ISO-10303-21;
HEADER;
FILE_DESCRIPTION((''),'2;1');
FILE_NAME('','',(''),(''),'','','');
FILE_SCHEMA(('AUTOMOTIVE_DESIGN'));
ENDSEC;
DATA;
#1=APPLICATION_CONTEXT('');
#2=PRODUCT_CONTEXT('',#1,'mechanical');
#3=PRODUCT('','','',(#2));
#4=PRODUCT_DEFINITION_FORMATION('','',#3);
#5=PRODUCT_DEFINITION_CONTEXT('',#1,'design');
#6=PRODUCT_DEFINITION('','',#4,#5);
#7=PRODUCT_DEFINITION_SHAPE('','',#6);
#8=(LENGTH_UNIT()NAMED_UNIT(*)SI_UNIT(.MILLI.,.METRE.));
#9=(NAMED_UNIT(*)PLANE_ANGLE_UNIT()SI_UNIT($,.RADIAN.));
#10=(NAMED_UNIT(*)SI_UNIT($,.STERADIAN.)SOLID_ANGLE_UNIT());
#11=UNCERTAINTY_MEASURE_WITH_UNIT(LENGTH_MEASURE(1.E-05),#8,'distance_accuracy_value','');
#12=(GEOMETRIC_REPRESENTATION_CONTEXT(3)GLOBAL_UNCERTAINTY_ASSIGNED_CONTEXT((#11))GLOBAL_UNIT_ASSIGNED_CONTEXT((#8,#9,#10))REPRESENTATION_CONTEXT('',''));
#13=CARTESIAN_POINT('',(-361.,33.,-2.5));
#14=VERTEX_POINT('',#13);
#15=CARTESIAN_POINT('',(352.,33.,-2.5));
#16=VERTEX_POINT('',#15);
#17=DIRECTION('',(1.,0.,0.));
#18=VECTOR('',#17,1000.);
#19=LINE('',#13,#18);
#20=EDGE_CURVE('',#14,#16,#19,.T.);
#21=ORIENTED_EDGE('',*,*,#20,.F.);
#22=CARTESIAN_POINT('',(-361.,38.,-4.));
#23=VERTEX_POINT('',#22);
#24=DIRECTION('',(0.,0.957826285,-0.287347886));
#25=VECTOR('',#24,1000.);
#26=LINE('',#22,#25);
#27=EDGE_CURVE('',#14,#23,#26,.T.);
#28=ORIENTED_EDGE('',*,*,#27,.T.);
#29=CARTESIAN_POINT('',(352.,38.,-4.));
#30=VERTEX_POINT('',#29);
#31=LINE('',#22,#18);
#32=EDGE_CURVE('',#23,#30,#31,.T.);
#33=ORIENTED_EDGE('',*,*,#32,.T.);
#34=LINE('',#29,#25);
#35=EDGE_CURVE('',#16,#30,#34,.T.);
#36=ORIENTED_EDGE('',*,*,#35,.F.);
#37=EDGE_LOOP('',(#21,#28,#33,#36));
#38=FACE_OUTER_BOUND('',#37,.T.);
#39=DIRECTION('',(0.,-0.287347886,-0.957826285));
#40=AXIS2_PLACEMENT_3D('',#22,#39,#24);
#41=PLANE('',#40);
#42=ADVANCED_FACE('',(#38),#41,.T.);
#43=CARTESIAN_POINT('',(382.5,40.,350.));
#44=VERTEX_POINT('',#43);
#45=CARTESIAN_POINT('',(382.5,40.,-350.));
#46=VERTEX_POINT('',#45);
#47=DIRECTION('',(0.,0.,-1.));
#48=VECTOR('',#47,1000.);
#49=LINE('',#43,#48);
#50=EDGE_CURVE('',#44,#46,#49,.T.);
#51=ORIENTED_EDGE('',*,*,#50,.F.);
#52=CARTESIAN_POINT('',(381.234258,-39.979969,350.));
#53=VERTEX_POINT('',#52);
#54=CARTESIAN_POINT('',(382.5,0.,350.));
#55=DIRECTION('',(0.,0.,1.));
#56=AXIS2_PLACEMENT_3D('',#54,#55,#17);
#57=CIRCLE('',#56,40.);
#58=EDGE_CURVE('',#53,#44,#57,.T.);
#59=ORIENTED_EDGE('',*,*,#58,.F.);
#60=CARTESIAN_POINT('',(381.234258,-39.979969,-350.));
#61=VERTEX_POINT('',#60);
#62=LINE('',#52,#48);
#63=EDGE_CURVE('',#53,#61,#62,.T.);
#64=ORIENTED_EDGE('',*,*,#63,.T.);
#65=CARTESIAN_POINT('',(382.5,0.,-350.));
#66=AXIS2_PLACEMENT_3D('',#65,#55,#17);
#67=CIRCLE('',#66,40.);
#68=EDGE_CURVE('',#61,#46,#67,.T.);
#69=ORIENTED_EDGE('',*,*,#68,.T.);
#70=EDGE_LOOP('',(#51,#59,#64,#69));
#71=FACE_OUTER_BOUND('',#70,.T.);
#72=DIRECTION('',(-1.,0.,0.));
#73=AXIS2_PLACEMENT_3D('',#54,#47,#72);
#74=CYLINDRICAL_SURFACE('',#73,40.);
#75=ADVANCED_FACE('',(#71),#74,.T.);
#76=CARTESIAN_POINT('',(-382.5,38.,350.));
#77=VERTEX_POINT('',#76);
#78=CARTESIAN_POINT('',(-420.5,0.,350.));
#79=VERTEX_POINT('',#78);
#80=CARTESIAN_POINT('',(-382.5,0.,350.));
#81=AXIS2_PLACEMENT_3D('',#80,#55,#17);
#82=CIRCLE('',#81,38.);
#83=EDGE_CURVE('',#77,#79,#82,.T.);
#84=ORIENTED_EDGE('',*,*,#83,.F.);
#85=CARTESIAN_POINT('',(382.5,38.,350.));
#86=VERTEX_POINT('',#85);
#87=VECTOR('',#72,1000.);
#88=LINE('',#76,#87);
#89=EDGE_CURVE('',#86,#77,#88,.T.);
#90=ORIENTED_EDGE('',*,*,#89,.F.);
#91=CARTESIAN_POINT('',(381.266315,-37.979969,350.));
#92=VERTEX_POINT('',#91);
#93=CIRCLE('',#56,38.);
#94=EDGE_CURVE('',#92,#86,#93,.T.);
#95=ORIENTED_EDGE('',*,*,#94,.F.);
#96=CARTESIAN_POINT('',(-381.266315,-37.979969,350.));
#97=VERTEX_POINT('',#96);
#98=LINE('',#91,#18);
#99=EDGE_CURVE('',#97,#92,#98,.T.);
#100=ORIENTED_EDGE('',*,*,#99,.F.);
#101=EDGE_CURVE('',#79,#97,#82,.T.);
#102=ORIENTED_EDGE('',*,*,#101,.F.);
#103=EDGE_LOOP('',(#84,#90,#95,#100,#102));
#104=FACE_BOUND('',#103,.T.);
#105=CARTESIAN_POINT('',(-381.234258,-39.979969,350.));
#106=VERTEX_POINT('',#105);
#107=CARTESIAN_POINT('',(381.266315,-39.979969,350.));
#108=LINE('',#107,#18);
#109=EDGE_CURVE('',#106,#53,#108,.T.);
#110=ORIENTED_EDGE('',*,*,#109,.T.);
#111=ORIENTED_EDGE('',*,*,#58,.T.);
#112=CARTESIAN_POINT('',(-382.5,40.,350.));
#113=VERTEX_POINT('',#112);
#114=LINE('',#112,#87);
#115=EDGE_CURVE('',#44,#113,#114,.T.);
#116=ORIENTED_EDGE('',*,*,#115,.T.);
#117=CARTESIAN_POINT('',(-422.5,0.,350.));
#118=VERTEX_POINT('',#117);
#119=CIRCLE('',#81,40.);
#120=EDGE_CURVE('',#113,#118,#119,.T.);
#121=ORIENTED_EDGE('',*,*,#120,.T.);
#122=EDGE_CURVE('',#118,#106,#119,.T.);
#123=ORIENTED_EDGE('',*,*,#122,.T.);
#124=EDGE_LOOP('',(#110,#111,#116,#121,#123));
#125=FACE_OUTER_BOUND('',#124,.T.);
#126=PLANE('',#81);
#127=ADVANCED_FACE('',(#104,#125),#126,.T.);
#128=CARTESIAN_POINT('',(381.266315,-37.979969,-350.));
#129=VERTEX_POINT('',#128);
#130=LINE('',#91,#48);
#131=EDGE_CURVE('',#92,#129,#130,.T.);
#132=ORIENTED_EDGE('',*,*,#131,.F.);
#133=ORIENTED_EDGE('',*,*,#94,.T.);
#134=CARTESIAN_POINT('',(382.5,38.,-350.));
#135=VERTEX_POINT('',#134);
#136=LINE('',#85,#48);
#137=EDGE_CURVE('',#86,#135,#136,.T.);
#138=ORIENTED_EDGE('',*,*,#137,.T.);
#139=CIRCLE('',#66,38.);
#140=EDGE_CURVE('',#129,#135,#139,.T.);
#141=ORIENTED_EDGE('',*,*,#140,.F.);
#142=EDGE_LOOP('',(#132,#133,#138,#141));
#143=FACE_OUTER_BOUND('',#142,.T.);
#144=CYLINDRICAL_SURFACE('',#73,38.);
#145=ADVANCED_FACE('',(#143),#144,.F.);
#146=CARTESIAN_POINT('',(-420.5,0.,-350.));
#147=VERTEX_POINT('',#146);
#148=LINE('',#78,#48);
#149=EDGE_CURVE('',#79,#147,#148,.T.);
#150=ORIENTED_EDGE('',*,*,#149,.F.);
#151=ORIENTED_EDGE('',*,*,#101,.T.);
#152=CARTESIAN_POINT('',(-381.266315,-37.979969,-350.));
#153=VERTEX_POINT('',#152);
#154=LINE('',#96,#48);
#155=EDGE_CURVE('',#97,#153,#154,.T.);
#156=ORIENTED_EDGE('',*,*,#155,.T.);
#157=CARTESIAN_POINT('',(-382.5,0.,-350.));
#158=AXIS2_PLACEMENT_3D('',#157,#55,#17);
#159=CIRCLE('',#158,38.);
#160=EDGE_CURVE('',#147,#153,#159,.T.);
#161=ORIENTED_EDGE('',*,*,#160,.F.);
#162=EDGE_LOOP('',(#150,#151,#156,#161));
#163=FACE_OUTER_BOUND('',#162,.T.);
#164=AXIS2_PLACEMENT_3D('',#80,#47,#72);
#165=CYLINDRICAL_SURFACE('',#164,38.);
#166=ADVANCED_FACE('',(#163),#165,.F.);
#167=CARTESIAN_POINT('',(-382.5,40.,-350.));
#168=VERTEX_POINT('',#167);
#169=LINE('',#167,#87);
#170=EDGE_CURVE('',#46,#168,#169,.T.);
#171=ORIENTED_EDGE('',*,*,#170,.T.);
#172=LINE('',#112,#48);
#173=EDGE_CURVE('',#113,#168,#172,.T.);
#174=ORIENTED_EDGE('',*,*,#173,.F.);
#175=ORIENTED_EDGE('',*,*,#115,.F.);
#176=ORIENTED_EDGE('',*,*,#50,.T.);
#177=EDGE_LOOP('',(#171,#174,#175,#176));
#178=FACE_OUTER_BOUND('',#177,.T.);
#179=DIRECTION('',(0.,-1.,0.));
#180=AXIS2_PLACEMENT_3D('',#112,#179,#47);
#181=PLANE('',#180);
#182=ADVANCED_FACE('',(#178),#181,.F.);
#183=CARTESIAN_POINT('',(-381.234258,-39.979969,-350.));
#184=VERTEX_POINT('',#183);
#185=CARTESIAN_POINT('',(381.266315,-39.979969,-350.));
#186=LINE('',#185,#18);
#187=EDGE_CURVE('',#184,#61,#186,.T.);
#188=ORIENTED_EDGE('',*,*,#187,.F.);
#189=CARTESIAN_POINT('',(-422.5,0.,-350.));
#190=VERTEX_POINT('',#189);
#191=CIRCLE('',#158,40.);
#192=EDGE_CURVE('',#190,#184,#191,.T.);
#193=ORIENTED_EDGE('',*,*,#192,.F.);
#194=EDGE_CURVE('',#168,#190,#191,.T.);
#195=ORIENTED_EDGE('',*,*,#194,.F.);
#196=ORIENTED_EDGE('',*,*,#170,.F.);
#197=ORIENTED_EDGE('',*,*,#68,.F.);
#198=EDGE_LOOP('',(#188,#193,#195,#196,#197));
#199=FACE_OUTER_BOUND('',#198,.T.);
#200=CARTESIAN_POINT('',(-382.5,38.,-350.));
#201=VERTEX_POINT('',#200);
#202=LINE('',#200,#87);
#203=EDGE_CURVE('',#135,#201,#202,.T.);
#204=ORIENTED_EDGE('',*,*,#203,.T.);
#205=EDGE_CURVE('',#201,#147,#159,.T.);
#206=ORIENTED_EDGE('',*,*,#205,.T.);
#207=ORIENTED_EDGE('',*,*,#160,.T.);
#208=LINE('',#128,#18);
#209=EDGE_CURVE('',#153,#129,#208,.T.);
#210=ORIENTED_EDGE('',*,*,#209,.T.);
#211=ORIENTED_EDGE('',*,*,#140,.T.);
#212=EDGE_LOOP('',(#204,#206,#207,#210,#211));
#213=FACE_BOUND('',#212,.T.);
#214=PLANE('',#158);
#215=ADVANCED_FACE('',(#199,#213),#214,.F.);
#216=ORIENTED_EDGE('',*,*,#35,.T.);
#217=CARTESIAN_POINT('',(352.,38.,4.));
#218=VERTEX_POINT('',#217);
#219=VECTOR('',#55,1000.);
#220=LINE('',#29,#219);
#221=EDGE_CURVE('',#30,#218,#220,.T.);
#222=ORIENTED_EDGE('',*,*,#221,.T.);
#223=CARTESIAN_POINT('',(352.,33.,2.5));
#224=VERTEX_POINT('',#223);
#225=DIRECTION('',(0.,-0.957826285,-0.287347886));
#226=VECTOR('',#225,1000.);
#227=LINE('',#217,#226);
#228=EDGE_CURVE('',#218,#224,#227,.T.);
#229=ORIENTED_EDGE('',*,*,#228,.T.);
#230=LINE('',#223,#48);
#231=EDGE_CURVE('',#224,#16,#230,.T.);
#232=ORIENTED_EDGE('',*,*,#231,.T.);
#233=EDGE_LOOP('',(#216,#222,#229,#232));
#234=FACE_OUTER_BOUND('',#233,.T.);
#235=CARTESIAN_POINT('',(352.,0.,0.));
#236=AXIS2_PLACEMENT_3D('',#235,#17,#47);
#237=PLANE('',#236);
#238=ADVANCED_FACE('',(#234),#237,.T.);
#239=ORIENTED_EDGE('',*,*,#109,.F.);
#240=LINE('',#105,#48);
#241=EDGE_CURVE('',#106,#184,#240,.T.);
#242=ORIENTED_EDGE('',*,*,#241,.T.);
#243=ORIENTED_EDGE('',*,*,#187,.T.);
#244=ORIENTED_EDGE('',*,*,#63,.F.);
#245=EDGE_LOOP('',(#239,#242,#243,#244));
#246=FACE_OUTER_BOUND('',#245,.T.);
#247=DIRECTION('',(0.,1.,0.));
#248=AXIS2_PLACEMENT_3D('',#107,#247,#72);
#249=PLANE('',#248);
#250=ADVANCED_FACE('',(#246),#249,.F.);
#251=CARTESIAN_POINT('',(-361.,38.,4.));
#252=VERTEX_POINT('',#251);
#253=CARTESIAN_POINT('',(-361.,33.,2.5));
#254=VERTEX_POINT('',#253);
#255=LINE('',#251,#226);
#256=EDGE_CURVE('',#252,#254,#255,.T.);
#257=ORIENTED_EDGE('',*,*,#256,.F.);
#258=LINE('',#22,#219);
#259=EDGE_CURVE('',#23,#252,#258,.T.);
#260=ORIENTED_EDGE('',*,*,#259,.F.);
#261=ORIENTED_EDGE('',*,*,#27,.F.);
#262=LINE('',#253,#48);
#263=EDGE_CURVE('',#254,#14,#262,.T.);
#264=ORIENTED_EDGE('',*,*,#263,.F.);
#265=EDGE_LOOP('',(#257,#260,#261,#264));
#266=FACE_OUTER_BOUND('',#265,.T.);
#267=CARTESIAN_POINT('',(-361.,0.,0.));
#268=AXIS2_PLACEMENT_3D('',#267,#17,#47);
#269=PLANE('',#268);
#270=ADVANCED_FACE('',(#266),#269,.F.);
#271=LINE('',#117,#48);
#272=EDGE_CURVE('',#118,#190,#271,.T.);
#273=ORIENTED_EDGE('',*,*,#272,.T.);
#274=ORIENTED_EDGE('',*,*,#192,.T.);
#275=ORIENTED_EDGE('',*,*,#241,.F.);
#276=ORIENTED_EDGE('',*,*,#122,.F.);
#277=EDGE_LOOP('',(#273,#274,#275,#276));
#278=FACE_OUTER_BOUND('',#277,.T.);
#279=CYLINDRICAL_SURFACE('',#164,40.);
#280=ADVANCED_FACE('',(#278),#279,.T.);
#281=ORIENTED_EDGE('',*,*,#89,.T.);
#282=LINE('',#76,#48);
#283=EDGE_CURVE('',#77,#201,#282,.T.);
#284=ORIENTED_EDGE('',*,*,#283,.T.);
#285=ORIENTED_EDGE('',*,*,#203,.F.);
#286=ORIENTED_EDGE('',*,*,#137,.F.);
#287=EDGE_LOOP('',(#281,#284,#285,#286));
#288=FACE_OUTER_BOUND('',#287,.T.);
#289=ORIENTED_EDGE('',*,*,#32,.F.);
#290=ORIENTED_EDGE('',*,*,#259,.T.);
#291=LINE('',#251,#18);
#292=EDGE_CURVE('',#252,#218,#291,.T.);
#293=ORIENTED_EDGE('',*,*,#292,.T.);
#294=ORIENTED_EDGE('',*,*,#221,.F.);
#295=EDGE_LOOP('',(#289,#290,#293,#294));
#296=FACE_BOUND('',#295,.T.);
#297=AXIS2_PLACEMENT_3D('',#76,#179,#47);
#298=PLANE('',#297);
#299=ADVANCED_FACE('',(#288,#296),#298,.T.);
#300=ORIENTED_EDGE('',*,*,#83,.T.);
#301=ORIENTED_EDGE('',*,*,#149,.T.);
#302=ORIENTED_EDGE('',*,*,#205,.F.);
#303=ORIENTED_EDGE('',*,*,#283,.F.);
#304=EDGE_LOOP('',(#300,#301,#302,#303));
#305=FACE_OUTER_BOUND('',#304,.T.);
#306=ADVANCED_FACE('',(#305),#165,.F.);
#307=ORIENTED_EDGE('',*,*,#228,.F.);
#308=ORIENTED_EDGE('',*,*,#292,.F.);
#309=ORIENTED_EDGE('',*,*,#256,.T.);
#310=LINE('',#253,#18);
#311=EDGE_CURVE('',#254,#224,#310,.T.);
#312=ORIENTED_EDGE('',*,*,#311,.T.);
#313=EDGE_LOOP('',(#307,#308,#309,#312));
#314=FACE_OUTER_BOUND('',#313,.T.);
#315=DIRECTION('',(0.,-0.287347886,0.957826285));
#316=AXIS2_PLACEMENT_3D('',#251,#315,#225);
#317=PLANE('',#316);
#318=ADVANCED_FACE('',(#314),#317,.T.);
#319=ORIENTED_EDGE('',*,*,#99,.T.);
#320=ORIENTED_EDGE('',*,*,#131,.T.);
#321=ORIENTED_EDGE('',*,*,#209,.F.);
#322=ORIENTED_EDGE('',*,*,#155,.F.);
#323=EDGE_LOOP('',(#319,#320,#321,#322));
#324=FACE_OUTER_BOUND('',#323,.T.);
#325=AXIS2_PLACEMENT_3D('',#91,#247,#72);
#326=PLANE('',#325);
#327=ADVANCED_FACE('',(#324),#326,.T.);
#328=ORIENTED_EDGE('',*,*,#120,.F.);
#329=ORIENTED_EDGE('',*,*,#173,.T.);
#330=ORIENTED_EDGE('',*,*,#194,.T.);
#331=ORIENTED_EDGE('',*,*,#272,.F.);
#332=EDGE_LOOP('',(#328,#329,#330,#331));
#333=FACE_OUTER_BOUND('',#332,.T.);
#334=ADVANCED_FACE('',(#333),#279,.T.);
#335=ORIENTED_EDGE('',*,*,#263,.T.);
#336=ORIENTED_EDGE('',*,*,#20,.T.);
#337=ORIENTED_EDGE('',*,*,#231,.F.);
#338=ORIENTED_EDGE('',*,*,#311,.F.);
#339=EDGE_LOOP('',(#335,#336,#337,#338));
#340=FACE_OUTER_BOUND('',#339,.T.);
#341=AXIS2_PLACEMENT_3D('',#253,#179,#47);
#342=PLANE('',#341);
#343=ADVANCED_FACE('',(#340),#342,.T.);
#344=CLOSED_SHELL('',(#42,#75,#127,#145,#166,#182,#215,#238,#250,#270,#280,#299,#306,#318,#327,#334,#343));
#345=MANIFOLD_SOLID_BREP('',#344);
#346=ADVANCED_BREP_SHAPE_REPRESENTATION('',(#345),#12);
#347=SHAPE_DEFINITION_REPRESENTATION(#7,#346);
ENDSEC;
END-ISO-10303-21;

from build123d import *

# Parameters (mm, degrees)
EXTRUDE_1_DEPTH      = 350
EXTRUDE_2_DEPTH      = 352
EXTRUDE_2_DEPTH_BACK = 361


with BuildPart() as part:
    # 草图1 → 拉伸-薄壁1 (new, symmetric)
    with BuildSketch(Plane.XY):
        with BuildLine():
            Line((381.234257801, -39.979968693), (-381.234257801, -39.979968693))
            ThreePointArc((-381.234257801, -39.979968693), (-422.49499186, -0.632950347), (-382.5, 40))
            Line((-382.5, 40), (382.5, 40))
            ThreePointArc((382.5, 40), (422.49499186, -0.632950347), (381.234257801, -39.979968693))
        make_face()
        with BuildLine():
            Line((381.26631524, -37.979968693), (-381.26631524, -37.979968693))
            ThreePointArc((-381.26631524, -37.979968693), (-420.494991843, -0.616923686), (-382.5, 38))
            Line((-382.5, 38), (382.5, 38))
            ThreePointArc((382.5, 38), (420.494991843, -0.616923686), (381.26631524, -37.979968693))
        make_face(mode=Mode.SUBTRACT)
    extrude(amount=EXTRUDE_1_DEPTH, both=True)

    # 草图4 → 凸台-拉伸2 (add, two sides: drawn at the far end of the back side and taken through both)
    with BuildSketch(Plane(origin=(0, 0, 0), x_dir=(0, 0, -1), z_dir=(1, 0, 0)).offset(-EXTRUDE_2_DEPTH_BACK)):
        Polygon((4, 38), (-4, 38), (-2.5, 33), (2.5, 33), align=None)
    extrude(amount=EXTRUDE_2_DEPTH + EXTRUDE_2_DEPTH_BACK)


solid = part.part
